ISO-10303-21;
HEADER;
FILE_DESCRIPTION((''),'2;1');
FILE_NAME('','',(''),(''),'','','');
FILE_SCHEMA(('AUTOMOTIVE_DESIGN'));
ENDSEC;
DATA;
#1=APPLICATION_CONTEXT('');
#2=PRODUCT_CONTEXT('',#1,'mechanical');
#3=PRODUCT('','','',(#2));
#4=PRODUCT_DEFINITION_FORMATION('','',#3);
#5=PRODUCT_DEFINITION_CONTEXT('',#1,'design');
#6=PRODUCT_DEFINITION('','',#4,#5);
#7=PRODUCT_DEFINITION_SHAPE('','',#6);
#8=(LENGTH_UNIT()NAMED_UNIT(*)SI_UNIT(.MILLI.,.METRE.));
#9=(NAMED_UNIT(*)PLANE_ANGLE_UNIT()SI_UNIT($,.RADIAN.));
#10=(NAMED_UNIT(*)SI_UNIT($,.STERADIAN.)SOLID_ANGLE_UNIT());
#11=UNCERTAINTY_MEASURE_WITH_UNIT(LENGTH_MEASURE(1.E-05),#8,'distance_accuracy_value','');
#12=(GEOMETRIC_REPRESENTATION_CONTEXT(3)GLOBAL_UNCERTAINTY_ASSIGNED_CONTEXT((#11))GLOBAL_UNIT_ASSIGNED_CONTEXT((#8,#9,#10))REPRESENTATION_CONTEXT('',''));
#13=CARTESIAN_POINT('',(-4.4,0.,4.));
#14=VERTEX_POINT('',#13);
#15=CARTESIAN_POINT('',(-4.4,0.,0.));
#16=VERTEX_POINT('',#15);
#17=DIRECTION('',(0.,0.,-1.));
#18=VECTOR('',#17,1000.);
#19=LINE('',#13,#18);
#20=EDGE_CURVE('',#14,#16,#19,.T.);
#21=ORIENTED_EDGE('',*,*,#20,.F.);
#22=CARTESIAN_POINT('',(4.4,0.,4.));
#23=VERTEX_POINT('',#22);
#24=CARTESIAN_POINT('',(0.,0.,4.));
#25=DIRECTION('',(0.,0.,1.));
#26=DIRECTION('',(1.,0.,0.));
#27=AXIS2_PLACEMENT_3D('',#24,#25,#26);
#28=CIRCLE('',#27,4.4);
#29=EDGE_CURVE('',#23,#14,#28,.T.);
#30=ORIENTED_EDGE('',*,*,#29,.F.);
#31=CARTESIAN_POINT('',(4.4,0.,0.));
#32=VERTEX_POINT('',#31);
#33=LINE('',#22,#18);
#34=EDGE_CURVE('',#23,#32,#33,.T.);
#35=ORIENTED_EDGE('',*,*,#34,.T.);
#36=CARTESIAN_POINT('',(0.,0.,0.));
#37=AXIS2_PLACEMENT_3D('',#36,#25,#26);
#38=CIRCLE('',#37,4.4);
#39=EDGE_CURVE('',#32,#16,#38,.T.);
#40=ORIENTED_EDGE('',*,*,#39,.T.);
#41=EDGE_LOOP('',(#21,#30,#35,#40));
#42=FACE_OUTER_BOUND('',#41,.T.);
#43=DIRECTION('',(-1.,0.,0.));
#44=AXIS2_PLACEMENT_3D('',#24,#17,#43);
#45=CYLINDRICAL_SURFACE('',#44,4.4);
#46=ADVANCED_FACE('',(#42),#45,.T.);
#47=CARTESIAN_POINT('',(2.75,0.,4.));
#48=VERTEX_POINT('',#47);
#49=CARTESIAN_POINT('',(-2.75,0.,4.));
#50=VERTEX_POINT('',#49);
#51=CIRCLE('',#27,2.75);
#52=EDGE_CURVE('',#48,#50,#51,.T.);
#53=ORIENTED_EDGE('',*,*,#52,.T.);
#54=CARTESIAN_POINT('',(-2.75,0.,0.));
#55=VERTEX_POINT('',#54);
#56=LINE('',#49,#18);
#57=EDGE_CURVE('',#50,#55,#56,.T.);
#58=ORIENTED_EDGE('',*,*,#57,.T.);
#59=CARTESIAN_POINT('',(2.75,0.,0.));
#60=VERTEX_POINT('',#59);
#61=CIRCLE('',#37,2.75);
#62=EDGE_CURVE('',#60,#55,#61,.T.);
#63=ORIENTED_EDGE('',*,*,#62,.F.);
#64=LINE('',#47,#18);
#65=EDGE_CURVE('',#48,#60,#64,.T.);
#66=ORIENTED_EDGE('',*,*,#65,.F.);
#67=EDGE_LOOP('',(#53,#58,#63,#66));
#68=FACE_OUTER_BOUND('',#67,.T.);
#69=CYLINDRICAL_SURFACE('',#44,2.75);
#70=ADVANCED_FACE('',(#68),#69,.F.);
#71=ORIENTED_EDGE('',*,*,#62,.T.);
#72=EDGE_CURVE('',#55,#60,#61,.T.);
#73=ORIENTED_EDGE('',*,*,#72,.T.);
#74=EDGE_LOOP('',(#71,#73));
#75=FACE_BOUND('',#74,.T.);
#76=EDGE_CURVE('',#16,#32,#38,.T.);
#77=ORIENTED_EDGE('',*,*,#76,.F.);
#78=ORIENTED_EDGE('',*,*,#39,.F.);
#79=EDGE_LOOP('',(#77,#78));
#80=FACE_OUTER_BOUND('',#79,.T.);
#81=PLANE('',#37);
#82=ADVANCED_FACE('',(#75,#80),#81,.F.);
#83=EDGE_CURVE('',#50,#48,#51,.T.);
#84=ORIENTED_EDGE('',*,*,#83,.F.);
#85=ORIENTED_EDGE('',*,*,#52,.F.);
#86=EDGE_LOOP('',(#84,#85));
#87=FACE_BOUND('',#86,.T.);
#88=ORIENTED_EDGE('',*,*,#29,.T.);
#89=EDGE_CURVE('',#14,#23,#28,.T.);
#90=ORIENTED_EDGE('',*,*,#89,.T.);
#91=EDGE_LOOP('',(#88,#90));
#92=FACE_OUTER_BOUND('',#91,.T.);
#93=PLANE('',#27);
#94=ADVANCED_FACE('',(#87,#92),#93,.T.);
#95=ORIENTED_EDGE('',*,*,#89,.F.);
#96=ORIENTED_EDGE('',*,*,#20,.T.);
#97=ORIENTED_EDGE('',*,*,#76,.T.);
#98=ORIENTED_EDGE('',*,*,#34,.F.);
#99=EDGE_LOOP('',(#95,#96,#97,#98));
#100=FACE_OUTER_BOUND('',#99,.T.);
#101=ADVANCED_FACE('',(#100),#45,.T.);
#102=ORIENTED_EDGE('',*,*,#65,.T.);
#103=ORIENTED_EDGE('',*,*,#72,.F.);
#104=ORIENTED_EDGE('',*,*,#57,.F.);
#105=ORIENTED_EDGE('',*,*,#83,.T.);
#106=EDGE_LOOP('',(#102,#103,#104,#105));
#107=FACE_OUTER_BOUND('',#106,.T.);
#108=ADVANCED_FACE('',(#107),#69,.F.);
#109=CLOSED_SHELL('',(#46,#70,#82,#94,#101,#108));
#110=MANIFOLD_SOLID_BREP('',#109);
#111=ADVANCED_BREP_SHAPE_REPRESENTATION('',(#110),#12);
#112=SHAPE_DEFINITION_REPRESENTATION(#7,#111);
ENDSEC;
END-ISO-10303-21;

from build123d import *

# Parameters (mm, degrees)
SKETCH1_R           = 4.4
SKETCH1_R_2         = 2.75
BOSS_EXTRUDE1_DEPTH = 4


with BuildPart() as part:
    # Sketch1 → Boss-Extrude1 (new body)
    with BuildSketch(Plane.XY):
        Circle(SKETCH1_R)
        Circle(SKETCH1_R_2, mode=Mode.SUBTRACT)
    extrude(amount=BOSS_EXTRUDE1_DEPTH)


solid = part.part
